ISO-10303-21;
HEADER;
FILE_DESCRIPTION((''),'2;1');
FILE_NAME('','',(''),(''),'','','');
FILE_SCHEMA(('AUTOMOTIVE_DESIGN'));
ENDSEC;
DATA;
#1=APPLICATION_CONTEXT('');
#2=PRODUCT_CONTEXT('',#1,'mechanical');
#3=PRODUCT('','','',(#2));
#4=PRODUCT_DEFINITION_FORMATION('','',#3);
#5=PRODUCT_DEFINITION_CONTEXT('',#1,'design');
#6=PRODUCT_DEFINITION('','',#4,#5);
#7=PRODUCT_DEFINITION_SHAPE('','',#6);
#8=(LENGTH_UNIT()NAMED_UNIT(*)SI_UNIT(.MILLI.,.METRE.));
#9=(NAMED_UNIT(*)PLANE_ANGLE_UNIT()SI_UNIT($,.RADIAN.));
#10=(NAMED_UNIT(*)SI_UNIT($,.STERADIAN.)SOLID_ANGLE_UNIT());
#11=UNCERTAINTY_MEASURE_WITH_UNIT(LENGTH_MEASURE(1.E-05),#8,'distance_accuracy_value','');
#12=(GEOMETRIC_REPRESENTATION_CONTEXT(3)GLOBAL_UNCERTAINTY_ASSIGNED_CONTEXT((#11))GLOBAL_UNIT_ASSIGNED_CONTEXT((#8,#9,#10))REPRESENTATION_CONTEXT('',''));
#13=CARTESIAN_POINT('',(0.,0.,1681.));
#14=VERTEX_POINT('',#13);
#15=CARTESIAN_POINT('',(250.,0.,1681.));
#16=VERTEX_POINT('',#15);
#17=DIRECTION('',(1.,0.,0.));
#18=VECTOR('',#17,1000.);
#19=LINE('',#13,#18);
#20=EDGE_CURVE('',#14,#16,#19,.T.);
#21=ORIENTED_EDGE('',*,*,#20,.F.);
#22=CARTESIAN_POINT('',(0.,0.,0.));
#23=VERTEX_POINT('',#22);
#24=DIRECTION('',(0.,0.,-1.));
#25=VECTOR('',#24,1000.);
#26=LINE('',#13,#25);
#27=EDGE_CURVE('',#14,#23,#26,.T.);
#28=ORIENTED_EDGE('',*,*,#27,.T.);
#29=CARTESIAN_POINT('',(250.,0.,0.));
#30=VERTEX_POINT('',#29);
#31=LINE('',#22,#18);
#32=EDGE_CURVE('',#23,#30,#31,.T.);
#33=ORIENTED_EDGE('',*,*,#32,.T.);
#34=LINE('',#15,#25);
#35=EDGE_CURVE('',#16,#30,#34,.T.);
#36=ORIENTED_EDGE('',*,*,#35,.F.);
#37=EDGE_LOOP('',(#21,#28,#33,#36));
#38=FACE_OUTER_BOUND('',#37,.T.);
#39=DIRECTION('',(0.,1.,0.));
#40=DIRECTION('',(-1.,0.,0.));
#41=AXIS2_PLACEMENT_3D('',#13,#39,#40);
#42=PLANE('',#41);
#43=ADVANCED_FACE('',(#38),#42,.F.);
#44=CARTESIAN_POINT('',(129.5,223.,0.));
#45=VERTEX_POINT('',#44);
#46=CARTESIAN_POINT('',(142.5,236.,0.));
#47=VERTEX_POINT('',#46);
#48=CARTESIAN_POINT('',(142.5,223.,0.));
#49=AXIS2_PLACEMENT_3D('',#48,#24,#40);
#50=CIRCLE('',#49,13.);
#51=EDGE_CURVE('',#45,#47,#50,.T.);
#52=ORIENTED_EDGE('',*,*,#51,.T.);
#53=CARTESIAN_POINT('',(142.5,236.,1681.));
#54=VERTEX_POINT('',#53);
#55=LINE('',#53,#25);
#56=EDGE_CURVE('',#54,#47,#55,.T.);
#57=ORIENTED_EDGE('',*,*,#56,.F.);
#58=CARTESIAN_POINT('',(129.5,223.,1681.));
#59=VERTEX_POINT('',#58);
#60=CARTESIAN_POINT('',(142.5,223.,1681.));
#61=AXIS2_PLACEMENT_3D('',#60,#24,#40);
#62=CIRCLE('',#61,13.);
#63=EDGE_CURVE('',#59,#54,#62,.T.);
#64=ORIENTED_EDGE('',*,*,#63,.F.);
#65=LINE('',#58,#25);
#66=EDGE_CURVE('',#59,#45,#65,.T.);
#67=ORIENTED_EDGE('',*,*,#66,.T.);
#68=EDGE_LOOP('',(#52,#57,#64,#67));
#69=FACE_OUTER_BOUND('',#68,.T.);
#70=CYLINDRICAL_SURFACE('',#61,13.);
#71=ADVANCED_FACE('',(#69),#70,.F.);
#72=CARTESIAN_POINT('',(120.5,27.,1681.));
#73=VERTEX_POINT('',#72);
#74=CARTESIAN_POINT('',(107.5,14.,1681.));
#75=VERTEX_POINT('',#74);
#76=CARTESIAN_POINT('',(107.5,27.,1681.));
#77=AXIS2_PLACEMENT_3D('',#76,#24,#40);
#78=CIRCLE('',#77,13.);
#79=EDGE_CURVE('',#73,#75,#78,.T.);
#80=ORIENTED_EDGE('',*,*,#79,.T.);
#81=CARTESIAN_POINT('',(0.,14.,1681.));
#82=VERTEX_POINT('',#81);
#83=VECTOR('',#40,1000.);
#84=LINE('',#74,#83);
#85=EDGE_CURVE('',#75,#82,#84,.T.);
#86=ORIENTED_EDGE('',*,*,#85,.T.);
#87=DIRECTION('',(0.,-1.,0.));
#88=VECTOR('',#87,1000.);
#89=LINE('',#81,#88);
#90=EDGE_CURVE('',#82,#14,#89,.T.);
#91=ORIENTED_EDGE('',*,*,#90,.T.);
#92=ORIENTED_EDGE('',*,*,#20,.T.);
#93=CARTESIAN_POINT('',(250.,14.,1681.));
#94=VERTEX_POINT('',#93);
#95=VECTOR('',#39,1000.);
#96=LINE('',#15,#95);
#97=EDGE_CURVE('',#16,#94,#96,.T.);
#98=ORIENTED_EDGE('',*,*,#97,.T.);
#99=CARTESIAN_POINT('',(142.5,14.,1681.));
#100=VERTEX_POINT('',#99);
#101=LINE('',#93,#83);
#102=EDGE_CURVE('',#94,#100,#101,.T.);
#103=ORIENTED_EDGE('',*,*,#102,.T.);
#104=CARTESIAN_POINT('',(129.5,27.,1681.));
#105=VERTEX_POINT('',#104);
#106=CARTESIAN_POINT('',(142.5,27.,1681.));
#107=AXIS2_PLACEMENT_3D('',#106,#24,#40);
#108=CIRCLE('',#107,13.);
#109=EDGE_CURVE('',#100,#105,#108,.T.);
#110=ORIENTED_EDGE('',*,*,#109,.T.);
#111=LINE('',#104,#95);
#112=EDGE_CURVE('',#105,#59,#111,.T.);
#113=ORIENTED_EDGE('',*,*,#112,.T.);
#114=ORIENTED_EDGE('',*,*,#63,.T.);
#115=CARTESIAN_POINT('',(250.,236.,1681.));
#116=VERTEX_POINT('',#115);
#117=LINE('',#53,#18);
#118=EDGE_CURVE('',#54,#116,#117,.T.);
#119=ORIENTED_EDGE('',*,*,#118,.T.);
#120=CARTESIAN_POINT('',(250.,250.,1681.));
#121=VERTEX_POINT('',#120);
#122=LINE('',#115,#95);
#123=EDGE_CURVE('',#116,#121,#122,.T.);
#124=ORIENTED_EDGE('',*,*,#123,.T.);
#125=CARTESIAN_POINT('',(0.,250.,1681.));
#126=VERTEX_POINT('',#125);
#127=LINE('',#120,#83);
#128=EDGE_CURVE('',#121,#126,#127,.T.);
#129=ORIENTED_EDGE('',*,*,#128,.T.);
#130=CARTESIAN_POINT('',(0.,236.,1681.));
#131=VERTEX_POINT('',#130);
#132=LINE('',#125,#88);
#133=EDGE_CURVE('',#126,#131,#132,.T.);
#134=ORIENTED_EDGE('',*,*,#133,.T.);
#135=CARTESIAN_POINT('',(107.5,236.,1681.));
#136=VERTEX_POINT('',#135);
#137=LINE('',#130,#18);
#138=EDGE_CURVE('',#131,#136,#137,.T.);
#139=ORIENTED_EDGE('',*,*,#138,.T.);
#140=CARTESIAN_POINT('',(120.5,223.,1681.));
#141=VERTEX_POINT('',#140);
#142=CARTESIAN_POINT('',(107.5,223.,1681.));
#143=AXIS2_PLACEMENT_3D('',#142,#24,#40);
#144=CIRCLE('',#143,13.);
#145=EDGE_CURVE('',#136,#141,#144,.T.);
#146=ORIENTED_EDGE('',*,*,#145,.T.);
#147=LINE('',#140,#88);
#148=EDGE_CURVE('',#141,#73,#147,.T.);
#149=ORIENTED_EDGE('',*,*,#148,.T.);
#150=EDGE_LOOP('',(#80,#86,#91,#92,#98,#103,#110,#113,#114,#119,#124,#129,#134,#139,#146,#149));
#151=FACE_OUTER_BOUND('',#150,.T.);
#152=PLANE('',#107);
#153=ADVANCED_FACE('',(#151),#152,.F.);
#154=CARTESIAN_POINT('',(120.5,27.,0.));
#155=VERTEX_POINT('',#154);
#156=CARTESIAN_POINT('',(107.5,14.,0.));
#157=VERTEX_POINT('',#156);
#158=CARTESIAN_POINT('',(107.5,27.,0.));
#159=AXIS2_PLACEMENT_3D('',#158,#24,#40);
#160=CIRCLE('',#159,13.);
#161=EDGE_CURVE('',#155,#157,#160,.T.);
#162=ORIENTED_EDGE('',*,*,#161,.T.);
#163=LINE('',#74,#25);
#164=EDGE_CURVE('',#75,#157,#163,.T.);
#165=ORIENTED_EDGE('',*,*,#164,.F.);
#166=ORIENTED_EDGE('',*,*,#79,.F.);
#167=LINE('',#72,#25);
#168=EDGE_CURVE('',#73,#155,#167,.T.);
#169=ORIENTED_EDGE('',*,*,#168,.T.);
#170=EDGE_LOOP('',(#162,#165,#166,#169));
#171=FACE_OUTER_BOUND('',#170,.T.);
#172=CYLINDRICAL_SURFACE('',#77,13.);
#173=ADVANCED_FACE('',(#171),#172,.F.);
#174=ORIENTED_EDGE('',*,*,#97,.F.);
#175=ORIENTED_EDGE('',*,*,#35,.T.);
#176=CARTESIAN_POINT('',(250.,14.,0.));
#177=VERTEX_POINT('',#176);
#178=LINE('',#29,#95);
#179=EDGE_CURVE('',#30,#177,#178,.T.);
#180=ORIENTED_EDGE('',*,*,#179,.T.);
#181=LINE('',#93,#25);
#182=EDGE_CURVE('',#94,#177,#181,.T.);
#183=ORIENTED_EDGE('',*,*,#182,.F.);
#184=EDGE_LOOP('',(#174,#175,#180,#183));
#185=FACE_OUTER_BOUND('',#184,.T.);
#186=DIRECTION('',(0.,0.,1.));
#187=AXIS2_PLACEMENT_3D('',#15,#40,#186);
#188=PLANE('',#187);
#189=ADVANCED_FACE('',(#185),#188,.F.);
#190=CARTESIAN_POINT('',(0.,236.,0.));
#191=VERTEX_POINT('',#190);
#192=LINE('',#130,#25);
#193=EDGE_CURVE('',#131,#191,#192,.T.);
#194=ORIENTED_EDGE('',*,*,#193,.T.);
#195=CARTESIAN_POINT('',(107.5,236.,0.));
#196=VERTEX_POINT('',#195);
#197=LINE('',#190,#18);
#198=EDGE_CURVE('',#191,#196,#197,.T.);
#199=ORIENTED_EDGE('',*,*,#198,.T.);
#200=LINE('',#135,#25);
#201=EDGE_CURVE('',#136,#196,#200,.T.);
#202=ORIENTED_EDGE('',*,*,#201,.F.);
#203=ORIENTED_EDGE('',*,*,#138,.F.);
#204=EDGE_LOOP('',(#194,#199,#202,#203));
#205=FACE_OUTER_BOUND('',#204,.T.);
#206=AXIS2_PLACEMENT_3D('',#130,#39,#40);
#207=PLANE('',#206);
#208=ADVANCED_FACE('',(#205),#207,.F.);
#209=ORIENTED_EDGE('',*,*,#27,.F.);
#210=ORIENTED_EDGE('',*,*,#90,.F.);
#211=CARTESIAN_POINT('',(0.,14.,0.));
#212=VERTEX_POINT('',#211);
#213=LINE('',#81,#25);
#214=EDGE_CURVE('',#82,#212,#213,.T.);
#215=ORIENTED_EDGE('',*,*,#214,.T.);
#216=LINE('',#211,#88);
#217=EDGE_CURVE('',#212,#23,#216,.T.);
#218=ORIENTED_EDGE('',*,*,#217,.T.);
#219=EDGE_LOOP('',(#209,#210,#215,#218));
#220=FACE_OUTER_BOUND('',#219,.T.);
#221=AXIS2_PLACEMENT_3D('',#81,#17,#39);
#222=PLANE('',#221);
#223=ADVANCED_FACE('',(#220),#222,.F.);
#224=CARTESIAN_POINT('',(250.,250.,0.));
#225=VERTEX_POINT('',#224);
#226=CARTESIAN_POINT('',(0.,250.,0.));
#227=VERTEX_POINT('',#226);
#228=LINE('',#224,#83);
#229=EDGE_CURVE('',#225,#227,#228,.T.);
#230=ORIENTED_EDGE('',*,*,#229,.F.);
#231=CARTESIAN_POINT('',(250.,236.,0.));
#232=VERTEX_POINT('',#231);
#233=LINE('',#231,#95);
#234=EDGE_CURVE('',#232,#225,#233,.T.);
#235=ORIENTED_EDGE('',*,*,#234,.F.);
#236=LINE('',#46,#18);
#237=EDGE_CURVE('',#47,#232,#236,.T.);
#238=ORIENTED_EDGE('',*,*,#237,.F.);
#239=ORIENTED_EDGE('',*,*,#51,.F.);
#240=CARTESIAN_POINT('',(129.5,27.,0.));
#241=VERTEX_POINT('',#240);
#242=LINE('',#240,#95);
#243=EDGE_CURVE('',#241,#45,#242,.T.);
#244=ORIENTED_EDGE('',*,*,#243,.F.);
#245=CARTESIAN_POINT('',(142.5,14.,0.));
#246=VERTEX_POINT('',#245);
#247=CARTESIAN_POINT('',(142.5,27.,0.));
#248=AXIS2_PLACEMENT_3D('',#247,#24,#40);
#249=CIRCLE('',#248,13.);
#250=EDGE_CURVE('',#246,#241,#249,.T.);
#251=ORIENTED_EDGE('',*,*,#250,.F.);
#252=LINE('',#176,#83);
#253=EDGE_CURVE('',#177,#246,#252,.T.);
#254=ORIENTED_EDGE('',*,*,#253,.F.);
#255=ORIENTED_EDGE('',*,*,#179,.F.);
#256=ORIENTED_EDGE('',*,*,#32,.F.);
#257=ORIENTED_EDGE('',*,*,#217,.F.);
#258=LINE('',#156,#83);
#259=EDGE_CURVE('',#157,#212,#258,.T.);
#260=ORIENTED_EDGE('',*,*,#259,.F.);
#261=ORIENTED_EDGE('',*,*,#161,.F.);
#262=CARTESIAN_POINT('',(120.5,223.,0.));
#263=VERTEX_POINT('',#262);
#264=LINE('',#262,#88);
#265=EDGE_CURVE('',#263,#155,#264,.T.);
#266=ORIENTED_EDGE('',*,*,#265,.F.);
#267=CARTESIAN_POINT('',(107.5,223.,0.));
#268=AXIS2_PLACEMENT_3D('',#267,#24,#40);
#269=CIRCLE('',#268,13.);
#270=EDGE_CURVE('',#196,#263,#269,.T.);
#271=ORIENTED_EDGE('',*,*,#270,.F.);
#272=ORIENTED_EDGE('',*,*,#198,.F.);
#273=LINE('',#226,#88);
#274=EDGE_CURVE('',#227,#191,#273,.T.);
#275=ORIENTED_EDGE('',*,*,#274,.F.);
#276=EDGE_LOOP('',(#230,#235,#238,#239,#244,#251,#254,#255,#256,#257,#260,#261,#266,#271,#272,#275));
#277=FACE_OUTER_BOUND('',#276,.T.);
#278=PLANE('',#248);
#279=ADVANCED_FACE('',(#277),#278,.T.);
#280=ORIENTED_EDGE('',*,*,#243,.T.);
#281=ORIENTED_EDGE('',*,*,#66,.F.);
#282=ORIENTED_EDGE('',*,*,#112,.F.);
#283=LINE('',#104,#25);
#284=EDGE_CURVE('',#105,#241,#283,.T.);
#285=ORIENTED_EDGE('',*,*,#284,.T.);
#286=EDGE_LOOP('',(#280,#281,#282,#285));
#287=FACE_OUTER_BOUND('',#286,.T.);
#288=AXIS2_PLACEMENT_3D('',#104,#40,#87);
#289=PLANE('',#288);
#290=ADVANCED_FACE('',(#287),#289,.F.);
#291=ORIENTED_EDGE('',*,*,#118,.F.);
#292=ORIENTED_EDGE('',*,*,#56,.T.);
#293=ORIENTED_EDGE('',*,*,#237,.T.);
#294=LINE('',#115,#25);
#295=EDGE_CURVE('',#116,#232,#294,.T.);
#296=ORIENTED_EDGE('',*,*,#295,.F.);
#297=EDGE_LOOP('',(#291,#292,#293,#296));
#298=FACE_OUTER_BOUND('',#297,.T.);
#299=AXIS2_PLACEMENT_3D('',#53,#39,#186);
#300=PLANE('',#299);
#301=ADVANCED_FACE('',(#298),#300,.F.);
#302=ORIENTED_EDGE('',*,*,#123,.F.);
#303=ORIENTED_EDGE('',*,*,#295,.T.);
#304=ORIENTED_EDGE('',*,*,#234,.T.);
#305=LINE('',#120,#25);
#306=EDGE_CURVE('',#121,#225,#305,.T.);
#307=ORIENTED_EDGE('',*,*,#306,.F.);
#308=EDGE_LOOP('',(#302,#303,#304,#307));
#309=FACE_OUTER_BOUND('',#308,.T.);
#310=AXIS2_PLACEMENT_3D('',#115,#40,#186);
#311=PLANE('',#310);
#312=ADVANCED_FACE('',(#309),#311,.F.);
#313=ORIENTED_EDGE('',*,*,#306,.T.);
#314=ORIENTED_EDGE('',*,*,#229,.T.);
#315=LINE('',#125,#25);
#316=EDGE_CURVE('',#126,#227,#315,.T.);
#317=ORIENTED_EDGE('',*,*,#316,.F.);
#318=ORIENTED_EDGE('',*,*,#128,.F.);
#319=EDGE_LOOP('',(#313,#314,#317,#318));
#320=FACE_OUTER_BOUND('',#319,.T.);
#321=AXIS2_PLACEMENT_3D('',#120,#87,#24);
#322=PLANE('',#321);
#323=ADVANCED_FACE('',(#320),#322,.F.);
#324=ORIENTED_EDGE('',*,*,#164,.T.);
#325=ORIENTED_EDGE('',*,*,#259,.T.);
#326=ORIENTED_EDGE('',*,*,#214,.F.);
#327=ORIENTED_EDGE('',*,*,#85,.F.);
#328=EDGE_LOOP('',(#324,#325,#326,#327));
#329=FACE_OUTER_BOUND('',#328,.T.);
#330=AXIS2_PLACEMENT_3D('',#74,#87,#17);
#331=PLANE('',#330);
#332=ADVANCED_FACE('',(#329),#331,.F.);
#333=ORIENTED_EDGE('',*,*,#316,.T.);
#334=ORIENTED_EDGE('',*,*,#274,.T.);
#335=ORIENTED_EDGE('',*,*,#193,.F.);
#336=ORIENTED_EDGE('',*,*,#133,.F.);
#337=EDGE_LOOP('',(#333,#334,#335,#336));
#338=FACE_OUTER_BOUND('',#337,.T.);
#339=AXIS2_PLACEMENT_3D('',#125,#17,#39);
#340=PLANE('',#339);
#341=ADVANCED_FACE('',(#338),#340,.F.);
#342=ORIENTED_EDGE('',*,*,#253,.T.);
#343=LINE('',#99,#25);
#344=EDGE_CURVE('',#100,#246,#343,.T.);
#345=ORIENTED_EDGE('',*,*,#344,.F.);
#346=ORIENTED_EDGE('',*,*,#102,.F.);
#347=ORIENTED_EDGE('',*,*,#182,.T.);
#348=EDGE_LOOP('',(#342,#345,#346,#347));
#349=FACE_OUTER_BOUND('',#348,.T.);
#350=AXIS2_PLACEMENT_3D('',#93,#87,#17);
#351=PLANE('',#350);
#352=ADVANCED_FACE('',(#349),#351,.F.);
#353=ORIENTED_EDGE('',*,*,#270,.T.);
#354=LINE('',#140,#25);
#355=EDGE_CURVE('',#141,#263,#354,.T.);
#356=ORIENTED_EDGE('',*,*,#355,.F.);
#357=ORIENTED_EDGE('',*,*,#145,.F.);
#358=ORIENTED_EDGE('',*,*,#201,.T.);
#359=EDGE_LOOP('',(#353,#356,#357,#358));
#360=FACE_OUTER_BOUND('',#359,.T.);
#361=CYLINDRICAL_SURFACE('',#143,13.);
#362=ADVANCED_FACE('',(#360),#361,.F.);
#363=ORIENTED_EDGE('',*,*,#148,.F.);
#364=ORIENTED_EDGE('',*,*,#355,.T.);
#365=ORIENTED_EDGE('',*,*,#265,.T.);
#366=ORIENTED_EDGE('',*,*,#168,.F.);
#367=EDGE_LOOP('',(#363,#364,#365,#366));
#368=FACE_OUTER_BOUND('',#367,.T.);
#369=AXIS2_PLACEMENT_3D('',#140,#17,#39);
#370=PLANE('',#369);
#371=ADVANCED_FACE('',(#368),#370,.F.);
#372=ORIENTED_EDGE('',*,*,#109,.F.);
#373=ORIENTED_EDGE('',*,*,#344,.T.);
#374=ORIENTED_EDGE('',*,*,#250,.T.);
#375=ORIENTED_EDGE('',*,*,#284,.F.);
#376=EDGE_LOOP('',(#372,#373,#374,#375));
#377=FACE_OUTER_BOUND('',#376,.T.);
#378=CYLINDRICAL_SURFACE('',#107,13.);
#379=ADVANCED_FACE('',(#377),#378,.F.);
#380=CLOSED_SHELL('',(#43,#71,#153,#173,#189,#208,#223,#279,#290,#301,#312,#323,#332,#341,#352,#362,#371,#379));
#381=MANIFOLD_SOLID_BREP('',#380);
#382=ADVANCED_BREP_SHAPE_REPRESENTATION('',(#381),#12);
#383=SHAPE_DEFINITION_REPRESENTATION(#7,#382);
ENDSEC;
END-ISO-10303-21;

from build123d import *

# Parameters (mm, degrees)
BOSS_EXTRUDE1_DEPTH = 1681


with BuildPart() as part:
    # Sketch1 → Boss-Extrude1 (new body)
    with BuildSketch(Plane.XY):
        with BuildLine():
            Line((0, 0), (250, 0))
            Line((250, 0), (250, 14))
            Line((250, 14), (142.5, 14))
            ThreePointArc((142.5, 14), (133.307611845, 17.807611845), (129.5, 27))
            Line((129.5, 27), (129.5, 223))
            ThreePointArc((129.5, 223), (133.307611845, 232.192388155), (142.5, 236))
            Line((142.5, 236), (250, 236))
            Line((250, 236), (250, 250))
            Line((250, 250), (0, 250))
            Line((0, 250), (0, 236))
            Line((0, 236), (107.5, 236))
            ThreePointArc((107.5, 236), (116.692388155, 232.192388155), (120.5, 223))
            Line((120.5, 223), (120.5, 27))
            ThreePointArc((120.5, 27), (116.692388155, 17.807611845), (107.5, 14))
            Line((107.5, 14), (0, 14))
            Line((0, 14), (0, 0))
        make_face()
    extrude(amount=BOSS_EXTRUDE1_DEPTH)


solid = part.part
